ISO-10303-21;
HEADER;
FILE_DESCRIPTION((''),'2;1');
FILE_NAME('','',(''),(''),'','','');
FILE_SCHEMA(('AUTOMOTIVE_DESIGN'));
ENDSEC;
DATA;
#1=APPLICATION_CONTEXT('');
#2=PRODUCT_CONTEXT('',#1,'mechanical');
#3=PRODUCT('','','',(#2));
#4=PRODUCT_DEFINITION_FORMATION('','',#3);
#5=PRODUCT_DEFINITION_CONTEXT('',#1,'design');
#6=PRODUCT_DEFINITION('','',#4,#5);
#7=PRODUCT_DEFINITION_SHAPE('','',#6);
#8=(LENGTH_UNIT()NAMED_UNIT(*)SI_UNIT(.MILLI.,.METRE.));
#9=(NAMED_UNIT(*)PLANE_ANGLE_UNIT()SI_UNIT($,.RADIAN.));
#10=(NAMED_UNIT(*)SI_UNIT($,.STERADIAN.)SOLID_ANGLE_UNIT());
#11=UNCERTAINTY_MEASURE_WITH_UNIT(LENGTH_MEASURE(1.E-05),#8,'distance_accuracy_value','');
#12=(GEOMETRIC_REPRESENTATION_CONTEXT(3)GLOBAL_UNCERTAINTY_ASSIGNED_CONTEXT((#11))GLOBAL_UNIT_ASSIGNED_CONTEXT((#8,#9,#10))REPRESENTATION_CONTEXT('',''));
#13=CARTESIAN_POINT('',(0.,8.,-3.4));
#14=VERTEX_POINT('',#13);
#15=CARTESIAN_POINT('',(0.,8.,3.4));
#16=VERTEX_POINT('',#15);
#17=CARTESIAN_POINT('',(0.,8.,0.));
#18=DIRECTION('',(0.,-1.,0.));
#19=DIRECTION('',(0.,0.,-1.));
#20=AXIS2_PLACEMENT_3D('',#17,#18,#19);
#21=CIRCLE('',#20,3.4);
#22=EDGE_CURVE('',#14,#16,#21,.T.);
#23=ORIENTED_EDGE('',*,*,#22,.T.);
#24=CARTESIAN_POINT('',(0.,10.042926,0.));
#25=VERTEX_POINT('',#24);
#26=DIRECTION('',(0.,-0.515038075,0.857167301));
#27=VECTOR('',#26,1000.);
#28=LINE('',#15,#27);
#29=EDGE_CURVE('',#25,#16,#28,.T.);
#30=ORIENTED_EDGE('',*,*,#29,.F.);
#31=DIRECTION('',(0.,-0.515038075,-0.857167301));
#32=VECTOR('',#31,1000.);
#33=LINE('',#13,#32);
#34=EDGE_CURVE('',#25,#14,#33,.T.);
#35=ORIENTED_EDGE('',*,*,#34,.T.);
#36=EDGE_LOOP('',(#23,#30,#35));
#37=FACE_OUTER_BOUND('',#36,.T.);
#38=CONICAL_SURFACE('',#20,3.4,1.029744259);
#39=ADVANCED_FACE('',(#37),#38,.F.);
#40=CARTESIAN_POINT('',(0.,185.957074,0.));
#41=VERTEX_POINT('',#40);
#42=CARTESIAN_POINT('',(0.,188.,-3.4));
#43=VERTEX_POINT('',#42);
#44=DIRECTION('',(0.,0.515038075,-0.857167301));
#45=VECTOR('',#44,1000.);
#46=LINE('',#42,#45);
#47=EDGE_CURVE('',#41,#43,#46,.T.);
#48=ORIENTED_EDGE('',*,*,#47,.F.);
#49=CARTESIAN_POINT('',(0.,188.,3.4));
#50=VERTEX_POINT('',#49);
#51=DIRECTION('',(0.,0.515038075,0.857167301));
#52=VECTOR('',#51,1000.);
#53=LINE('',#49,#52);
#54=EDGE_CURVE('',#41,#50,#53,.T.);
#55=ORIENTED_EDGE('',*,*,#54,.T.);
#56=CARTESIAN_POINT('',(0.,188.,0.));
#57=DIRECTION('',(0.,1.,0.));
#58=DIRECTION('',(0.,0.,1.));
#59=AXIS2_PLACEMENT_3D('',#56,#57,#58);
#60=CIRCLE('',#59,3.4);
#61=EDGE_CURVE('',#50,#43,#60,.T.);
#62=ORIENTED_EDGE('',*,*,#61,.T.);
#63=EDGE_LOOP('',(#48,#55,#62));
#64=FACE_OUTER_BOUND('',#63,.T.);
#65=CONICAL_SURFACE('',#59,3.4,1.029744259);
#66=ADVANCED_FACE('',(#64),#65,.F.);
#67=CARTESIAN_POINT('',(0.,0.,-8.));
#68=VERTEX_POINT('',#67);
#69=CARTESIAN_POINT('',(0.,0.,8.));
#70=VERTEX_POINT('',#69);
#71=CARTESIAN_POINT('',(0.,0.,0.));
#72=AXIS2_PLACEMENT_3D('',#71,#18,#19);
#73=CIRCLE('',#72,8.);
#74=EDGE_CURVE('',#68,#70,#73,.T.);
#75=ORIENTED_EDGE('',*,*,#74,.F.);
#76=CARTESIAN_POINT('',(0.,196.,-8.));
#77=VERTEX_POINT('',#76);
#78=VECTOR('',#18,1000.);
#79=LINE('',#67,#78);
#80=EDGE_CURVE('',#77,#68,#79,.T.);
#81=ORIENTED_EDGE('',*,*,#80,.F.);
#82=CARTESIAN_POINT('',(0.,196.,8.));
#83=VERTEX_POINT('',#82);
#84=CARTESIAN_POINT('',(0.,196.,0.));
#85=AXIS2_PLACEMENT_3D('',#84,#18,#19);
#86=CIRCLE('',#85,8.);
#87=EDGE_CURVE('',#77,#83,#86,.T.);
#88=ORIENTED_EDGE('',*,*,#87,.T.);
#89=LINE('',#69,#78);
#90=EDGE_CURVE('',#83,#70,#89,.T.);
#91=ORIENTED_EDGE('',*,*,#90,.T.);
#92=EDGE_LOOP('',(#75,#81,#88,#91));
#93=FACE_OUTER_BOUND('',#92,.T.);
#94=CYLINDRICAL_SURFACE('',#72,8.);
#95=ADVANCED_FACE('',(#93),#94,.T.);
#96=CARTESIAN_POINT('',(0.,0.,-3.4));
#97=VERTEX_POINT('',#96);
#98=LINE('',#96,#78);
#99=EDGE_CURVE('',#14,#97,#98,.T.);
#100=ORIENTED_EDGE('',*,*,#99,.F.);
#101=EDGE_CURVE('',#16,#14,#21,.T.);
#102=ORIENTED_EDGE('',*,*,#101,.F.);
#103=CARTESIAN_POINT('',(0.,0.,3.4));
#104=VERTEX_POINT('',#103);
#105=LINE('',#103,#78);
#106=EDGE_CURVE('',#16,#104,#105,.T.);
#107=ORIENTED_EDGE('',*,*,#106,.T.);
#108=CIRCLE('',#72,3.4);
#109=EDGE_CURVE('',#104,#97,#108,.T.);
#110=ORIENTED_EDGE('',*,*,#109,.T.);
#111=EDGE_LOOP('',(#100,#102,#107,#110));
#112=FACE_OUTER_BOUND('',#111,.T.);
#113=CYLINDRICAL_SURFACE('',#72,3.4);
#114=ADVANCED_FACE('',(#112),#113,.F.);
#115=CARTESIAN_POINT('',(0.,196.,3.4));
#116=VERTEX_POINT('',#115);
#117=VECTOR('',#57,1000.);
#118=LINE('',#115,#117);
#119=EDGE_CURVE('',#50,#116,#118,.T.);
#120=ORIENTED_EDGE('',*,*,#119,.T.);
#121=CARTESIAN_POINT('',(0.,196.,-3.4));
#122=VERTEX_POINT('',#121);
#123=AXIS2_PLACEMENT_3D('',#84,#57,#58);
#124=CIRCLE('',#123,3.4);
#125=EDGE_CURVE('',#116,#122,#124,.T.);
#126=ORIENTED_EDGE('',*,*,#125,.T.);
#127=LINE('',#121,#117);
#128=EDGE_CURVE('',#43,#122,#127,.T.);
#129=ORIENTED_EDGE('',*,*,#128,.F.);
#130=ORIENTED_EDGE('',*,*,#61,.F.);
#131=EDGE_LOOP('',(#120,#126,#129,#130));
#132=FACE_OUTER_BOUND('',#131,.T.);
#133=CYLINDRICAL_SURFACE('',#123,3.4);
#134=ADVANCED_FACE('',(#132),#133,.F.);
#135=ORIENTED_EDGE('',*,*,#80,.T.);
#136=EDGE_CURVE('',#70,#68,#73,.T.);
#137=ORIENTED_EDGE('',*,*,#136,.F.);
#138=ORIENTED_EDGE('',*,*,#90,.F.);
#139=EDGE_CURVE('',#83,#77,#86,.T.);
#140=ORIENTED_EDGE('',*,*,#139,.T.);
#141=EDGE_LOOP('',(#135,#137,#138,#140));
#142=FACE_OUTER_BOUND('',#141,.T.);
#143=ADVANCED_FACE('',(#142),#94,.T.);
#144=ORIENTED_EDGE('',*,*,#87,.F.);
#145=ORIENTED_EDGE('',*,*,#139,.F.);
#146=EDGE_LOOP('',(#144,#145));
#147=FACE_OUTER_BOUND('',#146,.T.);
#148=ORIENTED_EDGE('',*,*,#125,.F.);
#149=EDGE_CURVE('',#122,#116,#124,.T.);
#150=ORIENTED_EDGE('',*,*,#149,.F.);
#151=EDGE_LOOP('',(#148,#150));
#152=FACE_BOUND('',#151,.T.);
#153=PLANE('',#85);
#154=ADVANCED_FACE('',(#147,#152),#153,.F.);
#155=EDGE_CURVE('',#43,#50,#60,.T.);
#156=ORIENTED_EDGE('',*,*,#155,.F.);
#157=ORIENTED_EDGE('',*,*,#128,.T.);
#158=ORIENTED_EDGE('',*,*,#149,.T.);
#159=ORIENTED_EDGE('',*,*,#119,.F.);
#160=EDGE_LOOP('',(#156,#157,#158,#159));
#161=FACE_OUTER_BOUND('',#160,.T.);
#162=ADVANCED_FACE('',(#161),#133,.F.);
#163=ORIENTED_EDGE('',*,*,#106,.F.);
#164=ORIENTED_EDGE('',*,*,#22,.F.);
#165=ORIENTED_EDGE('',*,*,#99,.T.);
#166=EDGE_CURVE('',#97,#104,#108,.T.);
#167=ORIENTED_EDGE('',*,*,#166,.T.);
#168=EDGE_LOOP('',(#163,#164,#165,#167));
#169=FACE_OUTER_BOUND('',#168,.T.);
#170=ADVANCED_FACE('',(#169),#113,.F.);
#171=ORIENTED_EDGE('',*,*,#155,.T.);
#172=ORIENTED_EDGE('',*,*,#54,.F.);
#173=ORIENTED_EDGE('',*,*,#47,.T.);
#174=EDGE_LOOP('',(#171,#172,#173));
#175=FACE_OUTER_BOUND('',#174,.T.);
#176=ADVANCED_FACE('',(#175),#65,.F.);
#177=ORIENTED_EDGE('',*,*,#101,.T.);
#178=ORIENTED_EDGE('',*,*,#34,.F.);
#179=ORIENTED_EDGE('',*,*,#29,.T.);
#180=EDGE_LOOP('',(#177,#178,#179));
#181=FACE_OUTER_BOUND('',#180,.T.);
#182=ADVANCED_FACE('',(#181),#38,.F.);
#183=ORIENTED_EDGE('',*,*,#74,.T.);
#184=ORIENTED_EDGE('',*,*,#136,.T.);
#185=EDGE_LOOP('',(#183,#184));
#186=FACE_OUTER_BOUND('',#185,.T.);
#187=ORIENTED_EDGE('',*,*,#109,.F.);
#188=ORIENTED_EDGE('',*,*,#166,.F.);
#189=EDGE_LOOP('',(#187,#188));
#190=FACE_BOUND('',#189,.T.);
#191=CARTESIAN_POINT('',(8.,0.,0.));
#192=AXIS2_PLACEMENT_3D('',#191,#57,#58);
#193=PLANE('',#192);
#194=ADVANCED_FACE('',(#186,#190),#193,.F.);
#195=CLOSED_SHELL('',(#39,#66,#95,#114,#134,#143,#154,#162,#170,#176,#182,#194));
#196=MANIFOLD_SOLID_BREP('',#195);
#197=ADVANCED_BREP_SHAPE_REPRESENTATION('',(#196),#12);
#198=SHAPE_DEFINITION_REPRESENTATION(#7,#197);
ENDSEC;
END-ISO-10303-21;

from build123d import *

# Parameters (mm, degrees)
SKETCH_1_W             = 8
SKETCH_1_H             = 196
HOLE_WIZARD_M8_1_D     = 6.8
HOLE_WIZARD_M8_1_DEPTH = 8
HOLE_WIZARD_M8_1_TIP   = 2.042926105
HOLE_WIZARD_M8_2_D     = 6.8
HOLE_WIZARD_M8_2_DEPTH = 8
HOLE_WIZARD_M8_2_TIP   = 2.042926105


with BuildPart() as part:
    # 草图1 → 旋转-薄壁1 (revolve)
    with BuildSketch(Plane.XY, mode=Mode.PRIVATE) as revolve_1_sk:
        with Locations((-4, 98)):
            Rectangle(SKETCH_1_W, SKETCH_1_H)
    revolve(revolve_1_sk.sketch.rotate(Axis((0, 0, 0), (0, 1, 0)), 270), axis=Axis((0, 0, 0), (0, 1, 0)))

    # M8 螺纹孔的螺纹孔钻头1
    with Locations(Plane(origin=(0, 0, 0), x_dir=(-1, 0, 0), z_dir=(0, -1, 0))):
        with Locations((0, 0)):
            Hole(HOLE_WIZARD_M8_1_D / 2, depth=HOLE_WIZARD_M8_1_DEPTH)
            with Locations((0, 0, -(HOLE_WIZARD_M8_1_DEPTH + HOLE_WIZARD_M8_1_TIP / 2))):  # 118° drill point
                Cone(0, HOLE_WIZARD_M8_1_D / 2, HOLE_WIZARD_M8_1_TIP, mode=Mode.SUBTRACT)

    # M8 螺纹孔的螺纹孔钻头2
    with Locations(Plane(origin=(0, 196, 0), x_dir=(1, 0, 0), z_dir=(0, 1, 0))):
        with Locations((0, 0)):
            Hole(HOLE_WIZARD_M8_2_D / 2, depth=HOLE_WIZARD_M8_2_DEPTH)
            with Locations((0, 0, -(HOLE_WIZARD_M8_2_DEPTH + HOLE_WIZARD_M8_2_TIP / 2))):  # 118° drill point
                Cone(0, HOLE_WIZARD_M8_2_D / 2, HOLE_WIZARD_M8_2_TIP, mode=Mode.SUBTRACT)


solid = part.part
